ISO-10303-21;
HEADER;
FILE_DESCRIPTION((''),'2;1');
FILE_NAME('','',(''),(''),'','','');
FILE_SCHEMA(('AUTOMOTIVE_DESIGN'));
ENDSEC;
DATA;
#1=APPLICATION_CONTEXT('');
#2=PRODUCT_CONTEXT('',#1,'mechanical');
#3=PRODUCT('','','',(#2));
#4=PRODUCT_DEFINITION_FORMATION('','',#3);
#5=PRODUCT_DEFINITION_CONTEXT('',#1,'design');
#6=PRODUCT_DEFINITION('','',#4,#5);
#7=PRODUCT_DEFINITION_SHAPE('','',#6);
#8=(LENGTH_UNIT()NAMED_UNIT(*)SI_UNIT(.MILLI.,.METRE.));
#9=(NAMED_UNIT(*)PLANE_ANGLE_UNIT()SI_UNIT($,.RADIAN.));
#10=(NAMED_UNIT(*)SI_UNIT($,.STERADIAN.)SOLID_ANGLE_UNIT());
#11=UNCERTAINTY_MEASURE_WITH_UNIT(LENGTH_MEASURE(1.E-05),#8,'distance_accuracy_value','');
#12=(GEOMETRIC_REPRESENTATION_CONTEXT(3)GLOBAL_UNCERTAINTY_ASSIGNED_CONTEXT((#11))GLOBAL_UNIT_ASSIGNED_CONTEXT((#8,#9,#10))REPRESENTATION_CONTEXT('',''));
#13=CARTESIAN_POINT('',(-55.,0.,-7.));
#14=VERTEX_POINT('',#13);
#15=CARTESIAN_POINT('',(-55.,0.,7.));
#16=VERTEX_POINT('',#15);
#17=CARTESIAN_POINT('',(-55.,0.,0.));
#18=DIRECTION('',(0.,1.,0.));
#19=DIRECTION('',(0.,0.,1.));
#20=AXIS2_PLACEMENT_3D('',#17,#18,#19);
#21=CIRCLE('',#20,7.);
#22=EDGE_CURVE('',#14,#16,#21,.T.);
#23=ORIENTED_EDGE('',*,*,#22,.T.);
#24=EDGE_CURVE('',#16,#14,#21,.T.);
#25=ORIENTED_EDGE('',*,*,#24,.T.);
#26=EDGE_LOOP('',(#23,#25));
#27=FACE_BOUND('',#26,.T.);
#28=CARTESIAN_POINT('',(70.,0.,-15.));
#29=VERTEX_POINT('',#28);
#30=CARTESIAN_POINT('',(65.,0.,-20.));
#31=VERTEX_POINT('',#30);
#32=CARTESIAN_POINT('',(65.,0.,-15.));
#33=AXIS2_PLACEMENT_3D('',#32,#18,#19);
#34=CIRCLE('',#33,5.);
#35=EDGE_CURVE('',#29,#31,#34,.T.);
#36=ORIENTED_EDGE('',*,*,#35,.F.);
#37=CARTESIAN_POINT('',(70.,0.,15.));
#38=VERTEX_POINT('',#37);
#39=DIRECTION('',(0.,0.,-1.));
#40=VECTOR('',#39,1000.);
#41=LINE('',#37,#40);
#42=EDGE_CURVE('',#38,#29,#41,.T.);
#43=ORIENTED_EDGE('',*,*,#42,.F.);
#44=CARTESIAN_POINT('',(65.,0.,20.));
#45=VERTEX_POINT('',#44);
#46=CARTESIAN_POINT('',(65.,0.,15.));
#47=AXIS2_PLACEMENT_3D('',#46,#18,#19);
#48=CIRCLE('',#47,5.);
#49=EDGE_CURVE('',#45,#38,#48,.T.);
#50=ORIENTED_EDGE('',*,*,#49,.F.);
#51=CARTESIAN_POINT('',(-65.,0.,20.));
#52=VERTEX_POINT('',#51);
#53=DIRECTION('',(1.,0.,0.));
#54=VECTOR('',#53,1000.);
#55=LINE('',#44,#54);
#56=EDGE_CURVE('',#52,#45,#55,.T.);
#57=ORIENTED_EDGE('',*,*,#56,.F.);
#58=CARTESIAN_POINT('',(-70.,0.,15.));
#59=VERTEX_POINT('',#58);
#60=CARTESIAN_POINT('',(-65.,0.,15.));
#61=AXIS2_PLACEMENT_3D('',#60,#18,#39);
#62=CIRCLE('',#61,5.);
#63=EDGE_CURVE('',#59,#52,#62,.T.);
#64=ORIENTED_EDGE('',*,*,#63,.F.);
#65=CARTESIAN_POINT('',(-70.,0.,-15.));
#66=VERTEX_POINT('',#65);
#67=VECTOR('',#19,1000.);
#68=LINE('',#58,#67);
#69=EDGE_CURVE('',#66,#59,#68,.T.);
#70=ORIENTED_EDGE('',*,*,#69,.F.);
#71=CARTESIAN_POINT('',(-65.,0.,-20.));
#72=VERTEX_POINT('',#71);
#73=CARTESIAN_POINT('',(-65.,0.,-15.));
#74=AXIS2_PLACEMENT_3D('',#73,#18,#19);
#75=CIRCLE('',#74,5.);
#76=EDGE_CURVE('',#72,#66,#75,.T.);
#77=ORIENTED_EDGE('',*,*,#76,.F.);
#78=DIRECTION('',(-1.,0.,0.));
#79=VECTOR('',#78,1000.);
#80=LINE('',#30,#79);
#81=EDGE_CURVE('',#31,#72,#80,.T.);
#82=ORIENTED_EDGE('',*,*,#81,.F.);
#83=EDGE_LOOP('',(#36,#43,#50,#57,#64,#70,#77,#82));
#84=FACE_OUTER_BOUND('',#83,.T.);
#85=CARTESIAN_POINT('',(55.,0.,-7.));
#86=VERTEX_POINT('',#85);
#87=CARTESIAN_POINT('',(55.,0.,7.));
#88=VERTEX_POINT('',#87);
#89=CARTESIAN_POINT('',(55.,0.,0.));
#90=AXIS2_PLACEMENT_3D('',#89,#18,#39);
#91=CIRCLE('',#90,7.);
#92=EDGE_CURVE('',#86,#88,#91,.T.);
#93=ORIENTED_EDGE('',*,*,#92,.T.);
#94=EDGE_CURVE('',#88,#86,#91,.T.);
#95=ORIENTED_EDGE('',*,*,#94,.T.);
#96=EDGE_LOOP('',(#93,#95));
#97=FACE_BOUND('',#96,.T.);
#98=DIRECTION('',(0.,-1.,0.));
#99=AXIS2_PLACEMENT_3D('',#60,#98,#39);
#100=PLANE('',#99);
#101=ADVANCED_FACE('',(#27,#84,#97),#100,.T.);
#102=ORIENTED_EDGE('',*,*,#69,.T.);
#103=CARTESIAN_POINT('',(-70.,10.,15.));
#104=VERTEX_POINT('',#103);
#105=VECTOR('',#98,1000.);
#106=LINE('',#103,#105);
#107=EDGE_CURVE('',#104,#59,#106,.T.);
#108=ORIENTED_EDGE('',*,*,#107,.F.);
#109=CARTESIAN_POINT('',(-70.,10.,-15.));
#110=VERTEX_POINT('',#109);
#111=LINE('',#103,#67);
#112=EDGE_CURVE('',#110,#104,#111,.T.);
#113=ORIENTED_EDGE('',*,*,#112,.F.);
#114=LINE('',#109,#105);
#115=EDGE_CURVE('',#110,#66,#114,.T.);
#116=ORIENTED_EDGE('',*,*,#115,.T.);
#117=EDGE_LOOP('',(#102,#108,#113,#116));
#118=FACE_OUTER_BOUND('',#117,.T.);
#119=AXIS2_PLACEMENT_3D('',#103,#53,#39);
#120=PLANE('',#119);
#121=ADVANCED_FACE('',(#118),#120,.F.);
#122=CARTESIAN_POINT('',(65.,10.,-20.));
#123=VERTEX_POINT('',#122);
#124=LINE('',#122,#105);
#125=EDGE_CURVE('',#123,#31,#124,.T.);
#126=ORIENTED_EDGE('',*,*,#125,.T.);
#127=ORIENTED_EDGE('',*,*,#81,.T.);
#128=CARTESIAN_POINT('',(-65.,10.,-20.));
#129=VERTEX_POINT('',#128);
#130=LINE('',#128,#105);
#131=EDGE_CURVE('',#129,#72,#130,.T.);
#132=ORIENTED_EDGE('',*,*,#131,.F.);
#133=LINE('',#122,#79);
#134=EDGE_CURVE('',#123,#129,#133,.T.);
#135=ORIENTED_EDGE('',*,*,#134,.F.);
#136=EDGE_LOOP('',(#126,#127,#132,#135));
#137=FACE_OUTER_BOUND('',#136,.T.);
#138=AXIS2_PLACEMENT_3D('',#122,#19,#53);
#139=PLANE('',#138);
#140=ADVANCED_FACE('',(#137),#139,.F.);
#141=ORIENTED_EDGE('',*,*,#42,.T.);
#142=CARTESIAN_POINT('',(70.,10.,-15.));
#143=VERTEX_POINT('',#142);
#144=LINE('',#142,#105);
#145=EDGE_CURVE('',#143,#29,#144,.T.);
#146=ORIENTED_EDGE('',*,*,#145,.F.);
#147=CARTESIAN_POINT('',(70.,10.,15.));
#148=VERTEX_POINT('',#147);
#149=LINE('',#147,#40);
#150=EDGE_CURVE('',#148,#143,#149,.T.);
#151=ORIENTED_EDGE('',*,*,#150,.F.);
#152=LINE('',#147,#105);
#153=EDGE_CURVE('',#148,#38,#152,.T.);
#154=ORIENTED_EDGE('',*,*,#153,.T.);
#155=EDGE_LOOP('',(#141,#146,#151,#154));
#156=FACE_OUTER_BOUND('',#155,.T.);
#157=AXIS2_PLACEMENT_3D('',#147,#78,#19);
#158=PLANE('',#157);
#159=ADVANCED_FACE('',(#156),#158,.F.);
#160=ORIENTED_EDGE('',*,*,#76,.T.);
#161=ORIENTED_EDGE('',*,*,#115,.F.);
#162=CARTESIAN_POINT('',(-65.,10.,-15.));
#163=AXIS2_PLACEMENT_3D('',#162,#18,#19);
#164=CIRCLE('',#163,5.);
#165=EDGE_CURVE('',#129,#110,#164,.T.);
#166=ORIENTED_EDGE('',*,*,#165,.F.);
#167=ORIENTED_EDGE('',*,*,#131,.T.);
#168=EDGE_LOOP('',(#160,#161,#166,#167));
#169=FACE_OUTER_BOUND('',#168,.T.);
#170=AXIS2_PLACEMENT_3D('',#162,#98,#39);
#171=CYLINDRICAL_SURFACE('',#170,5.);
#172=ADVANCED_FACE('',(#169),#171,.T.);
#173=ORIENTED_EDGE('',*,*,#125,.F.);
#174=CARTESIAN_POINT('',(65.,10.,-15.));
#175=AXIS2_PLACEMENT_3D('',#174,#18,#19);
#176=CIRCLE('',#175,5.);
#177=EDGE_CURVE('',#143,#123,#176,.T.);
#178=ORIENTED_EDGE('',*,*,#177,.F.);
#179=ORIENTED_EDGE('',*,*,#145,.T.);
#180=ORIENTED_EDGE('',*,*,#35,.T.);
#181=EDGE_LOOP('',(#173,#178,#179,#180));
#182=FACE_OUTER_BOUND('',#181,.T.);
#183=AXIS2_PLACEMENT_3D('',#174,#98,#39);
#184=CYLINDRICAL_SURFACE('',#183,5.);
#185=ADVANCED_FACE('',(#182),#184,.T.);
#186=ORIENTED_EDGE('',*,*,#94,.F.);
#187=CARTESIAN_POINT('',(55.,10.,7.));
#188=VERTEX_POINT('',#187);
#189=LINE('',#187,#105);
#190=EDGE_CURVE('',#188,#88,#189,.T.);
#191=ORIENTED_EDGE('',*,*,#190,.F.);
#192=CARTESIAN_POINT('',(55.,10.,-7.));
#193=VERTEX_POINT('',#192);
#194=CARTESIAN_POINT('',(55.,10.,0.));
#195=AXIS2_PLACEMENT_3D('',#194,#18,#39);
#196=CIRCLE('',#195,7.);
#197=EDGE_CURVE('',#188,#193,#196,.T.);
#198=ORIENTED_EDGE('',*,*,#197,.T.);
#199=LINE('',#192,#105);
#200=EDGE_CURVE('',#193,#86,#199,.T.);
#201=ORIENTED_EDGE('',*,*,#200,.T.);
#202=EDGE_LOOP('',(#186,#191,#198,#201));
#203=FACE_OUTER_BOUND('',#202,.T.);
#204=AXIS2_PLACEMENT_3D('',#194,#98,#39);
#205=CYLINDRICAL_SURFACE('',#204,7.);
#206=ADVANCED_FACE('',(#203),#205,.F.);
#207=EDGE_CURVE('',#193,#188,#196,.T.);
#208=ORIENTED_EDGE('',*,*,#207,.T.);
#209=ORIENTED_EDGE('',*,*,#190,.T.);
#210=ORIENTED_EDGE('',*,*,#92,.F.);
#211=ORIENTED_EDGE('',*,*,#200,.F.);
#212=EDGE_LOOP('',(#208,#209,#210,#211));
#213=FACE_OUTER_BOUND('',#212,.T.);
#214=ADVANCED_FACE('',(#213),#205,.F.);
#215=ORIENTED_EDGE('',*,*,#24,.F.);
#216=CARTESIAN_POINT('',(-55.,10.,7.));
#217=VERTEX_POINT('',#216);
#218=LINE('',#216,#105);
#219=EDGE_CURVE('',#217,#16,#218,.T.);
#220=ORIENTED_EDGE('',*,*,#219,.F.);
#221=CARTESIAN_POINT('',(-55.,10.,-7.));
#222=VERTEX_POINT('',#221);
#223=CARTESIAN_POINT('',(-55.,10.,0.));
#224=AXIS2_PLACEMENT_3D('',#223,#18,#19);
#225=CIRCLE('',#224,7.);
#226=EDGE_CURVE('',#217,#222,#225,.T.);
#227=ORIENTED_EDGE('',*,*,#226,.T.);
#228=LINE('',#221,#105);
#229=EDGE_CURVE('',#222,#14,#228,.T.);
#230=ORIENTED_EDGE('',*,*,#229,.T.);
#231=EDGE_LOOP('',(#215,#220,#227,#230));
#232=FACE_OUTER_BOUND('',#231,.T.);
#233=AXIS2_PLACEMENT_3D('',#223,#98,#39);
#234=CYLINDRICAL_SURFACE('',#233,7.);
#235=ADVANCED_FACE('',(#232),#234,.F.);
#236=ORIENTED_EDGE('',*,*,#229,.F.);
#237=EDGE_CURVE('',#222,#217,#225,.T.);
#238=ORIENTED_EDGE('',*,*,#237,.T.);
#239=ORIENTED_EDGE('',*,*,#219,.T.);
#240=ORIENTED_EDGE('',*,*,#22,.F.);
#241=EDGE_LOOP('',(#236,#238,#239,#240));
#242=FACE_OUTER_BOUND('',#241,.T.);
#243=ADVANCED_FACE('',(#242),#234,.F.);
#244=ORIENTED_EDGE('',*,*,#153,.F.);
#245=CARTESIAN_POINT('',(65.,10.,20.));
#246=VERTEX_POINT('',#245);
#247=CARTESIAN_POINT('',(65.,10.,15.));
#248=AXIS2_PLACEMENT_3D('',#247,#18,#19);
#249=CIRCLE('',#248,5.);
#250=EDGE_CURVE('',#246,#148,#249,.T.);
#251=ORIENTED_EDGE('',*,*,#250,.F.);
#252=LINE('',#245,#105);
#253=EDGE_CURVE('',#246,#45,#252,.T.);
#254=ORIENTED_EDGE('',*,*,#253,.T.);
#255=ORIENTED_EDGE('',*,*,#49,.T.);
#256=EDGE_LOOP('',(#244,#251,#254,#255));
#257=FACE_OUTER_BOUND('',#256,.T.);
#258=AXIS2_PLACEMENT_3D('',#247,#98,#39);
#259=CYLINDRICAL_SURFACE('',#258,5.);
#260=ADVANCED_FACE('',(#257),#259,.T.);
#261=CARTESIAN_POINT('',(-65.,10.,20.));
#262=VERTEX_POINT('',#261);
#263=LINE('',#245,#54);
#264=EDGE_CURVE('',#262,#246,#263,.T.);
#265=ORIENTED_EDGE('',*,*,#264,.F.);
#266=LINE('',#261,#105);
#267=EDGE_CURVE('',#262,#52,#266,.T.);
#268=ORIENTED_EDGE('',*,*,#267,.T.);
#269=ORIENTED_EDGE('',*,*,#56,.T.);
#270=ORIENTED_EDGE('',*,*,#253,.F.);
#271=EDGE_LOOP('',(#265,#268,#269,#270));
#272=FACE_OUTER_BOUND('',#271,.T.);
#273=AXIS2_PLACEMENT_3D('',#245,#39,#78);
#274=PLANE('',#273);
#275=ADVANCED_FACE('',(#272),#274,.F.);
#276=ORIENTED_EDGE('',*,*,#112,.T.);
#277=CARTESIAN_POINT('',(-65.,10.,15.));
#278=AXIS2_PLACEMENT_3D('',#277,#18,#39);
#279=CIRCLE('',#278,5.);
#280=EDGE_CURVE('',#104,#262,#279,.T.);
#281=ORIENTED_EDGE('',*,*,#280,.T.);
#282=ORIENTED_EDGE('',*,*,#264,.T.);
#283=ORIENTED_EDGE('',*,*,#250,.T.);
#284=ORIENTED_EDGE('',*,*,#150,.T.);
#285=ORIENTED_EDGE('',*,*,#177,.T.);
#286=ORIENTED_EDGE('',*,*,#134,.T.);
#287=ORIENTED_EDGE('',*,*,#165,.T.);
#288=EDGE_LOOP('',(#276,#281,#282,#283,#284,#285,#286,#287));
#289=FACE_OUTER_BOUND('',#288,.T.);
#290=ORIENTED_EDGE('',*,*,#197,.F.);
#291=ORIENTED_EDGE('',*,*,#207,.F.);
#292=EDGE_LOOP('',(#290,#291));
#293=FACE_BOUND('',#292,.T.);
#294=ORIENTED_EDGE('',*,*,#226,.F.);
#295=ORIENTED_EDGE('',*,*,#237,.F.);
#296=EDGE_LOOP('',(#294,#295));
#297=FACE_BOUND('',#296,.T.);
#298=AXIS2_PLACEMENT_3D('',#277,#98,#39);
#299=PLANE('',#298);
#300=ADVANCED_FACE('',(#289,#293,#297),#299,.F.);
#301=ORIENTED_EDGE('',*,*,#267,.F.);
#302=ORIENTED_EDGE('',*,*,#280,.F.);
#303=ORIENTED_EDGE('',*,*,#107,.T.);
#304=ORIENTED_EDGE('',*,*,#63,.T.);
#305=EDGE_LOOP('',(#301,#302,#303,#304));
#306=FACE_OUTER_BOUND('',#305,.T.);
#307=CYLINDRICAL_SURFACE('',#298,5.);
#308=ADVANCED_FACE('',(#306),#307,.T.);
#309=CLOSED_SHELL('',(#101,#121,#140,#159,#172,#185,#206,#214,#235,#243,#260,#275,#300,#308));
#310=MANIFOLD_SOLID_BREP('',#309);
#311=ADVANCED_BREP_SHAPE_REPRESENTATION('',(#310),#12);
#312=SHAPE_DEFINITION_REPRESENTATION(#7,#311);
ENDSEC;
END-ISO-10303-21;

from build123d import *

# Parameters (mm, degrees)
SKETCH2_R           = 7
BOSS_EXTRUDE1_DEPTH = 10


with BuildPart() as part:
    # Sketch2 → Boss-Extrude1 (new body)
    with BuildSketch(Plane(origin=(0, 0, 0), x_dir=(1, 0, 0), z_dir=(0, 1, 0))):
        with BuildLine():
            Line((65, -20), (-65, -20))
            ThreePointArc((-65, -20), (-68.535533906, -18.535533906), (-70, -15))
            Line((-70, -15), (-70, 15))
            ThreePointArc((-70, 15), (-68.535533906, 18.535533906), (-65, 20))
            Line((-65, 20), (65, 20))
            ThreePointArc((65, 20), (68.535533906, 18.535533906), (70, 15))
            Line((70, 15), (70, -15))
            ThreePointArc((70, -15), (68.535533906, -18.535533906), (65, -20))
        make_face()
        with Locations(Location((-55, 0, 0), (0, 0, 270))):
            Circle(SKETCH2_R, mode=Mode.SUBTRACT)
        with Locations(Location((55, 0, 0), (0, 0, 90))):
            Circle(SKETCH2_R, mode=Mode.SUBTRACT)
    extrude(amount=BOSS_EXTRUDE1_DEPTH)


solid = part.part
